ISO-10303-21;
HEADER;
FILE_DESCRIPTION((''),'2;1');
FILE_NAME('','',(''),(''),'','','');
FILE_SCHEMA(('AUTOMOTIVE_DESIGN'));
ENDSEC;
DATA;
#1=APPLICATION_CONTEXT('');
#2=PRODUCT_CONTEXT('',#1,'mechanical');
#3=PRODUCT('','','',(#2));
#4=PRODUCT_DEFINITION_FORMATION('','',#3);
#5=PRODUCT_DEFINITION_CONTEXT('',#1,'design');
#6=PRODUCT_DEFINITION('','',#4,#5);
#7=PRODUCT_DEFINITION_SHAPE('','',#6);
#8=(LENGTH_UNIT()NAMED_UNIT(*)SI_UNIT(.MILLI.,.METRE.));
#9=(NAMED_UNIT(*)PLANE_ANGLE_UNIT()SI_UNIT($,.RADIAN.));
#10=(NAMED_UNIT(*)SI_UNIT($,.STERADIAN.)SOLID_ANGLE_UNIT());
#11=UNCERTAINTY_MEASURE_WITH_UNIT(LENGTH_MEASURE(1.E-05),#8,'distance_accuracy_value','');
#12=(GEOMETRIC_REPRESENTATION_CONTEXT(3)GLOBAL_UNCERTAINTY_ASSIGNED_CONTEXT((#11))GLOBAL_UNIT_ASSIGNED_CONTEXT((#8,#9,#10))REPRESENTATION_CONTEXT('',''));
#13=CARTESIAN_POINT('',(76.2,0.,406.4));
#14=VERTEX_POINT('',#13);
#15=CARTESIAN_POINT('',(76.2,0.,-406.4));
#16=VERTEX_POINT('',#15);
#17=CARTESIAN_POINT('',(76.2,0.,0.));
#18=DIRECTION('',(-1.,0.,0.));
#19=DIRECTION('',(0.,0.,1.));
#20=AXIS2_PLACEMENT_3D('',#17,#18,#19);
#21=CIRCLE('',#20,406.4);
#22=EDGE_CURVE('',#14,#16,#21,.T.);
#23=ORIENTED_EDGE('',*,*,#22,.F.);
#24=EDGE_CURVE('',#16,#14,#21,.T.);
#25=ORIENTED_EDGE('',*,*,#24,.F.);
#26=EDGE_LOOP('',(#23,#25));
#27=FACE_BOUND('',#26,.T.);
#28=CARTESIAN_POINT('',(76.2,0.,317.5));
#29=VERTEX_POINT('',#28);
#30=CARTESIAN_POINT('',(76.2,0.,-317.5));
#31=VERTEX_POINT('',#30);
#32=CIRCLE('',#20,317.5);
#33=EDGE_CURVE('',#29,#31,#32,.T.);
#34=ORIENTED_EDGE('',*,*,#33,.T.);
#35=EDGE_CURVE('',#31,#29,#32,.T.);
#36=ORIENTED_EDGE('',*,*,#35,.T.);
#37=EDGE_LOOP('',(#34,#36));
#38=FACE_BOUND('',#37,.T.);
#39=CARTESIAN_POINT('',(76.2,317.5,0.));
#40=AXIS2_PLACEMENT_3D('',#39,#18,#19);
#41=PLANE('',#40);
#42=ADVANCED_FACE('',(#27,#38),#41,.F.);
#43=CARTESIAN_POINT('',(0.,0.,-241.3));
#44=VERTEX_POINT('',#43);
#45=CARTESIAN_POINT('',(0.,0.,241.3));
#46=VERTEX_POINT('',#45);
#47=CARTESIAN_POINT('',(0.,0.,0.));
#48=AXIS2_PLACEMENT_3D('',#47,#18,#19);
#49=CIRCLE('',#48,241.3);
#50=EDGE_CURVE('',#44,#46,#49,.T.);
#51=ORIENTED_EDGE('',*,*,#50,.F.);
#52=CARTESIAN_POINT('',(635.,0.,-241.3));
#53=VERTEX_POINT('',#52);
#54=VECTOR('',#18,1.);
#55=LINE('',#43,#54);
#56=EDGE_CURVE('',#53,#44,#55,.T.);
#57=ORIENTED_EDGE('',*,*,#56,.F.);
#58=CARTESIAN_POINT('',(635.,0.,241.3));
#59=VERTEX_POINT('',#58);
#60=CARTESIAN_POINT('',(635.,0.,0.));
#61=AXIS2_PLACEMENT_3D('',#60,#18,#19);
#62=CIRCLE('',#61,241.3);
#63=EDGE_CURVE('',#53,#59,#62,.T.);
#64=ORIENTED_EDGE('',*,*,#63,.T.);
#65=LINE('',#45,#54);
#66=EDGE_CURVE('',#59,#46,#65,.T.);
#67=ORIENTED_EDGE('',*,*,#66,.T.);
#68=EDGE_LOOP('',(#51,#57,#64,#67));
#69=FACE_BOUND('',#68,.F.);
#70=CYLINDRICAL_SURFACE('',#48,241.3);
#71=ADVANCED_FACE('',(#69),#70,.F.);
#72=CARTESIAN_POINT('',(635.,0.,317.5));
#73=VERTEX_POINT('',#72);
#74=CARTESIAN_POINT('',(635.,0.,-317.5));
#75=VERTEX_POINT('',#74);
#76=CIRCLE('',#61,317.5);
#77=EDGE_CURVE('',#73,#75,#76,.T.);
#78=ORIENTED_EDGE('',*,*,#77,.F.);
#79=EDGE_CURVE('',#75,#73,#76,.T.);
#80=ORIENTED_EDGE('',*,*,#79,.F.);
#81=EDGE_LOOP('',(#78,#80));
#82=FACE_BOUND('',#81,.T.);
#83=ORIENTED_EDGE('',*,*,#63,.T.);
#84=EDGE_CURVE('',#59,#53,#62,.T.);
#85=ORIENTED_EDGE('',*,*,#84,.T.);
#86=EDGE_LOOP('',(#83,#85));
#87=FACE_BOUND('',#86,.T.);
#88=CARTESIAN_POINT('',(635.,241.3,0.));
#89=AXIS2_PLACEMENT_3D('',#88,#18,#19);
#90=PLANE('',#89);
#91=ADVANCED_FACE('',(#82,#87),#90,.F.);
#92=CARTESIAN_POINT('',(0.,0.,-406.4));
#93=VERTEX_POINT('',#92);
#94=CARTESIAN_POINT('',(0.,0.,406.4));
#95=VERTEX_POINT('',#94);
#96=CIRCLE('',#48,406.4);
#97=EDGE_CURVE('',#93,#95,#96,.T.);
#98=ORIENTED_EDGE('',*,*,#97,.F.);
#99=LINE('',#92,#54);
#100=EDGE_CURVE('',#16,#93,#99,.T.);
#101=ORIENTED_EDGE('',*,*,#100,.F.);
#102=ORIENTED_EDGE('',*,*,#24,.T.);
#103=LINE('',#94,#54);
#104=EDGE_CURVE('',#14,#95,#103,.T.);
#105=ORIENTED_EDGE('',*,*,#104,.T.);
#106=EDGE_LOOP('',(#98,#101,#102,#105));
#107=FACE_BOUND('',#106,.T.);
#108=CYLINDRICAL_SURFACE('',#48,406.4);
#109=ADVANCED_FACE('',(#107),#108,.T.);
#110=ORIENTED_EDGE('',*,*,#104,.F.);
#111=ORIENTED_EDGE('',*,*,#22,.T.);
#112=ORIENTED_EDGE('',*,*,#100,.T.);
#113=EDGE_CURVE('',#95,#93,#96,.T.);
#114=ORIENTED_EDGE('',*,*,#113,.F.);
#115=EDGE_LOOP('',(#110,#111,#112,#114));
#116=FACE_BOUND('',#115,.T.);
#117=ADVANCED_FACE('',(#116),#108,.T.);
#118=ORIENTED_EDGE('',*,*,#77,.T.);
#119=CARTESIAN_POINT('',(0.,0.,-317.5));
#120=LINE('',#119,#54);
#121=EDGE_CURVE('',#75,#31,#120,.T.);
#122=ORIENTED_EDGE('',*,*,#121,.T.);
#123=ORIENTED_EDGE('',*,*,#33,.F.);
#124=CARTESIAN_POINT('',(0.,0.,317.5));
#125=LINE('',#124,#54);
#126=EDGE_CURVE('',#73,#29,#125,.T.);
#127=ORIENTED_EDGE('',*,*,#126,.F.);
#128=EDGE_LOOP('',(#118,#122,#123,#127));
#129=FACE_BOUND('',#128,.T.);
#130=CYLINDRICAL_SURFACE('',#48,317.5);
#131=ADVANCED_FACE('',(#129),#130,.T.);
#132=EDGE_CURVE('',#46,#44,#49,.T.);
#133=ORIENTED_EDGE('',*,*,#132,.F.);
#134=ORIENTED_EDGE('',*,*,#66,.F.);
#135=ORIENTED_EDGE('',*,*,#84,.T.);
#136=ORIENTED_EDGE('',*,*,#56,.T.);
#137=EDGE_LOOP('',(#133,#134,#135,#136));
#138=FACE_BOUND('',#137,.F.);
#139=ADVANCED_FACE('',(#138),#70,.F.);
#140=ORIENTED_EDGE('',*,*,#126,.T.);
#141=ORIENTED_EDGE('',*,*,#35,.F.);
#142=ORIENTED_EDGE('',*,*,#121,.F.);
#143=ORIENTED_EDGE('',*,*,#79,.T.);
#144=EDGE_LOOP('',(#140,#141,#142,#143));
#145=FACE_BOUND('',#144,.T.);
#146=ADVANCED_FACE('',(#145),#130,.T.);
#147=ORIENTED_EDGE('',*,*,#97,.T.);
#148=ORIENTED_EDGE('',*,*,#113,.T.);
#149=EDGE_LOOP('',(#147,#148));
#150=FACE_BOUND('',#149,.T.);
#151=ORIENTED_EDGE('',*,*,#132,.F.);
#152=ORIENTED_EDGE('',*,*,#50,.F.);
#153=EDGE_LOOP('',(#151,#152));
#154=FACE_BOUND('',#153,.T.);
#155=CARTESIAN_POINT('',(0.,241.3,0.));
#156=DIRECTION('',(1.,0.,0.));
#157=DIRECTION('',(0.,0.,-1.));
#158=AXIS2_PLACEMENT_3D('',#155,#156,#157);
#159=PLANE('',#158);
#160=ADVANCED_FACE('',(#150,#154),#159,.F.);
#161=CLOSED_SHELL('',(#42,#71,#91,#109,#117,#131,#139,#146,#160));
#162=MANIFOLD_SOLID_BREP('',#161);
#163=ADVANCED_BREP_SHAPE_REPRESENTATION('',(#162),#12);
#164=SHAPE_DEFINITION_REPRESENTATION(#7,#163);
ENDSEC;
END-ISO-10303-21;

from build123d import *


with BuildPart() as part:
    # Sketch1 → Revolve1 (revolve)
    with BuildSketch(Plane.XY, mode=Mode.PRIVATE) as revolve1_sk:
        Polygon((0, 241.3), (0, 406.4), (76.2, 406.4), (76.2, 317.5), (635, 317.5), (635, 241.3), align=None)
    revolve(revolve1_sk.sketch.rotate(Axis((0, 0, 0), (1, 0, 0)), 90), axis=Axis((0, 0, 0), (1, 0, 0)))


solid = part.part
